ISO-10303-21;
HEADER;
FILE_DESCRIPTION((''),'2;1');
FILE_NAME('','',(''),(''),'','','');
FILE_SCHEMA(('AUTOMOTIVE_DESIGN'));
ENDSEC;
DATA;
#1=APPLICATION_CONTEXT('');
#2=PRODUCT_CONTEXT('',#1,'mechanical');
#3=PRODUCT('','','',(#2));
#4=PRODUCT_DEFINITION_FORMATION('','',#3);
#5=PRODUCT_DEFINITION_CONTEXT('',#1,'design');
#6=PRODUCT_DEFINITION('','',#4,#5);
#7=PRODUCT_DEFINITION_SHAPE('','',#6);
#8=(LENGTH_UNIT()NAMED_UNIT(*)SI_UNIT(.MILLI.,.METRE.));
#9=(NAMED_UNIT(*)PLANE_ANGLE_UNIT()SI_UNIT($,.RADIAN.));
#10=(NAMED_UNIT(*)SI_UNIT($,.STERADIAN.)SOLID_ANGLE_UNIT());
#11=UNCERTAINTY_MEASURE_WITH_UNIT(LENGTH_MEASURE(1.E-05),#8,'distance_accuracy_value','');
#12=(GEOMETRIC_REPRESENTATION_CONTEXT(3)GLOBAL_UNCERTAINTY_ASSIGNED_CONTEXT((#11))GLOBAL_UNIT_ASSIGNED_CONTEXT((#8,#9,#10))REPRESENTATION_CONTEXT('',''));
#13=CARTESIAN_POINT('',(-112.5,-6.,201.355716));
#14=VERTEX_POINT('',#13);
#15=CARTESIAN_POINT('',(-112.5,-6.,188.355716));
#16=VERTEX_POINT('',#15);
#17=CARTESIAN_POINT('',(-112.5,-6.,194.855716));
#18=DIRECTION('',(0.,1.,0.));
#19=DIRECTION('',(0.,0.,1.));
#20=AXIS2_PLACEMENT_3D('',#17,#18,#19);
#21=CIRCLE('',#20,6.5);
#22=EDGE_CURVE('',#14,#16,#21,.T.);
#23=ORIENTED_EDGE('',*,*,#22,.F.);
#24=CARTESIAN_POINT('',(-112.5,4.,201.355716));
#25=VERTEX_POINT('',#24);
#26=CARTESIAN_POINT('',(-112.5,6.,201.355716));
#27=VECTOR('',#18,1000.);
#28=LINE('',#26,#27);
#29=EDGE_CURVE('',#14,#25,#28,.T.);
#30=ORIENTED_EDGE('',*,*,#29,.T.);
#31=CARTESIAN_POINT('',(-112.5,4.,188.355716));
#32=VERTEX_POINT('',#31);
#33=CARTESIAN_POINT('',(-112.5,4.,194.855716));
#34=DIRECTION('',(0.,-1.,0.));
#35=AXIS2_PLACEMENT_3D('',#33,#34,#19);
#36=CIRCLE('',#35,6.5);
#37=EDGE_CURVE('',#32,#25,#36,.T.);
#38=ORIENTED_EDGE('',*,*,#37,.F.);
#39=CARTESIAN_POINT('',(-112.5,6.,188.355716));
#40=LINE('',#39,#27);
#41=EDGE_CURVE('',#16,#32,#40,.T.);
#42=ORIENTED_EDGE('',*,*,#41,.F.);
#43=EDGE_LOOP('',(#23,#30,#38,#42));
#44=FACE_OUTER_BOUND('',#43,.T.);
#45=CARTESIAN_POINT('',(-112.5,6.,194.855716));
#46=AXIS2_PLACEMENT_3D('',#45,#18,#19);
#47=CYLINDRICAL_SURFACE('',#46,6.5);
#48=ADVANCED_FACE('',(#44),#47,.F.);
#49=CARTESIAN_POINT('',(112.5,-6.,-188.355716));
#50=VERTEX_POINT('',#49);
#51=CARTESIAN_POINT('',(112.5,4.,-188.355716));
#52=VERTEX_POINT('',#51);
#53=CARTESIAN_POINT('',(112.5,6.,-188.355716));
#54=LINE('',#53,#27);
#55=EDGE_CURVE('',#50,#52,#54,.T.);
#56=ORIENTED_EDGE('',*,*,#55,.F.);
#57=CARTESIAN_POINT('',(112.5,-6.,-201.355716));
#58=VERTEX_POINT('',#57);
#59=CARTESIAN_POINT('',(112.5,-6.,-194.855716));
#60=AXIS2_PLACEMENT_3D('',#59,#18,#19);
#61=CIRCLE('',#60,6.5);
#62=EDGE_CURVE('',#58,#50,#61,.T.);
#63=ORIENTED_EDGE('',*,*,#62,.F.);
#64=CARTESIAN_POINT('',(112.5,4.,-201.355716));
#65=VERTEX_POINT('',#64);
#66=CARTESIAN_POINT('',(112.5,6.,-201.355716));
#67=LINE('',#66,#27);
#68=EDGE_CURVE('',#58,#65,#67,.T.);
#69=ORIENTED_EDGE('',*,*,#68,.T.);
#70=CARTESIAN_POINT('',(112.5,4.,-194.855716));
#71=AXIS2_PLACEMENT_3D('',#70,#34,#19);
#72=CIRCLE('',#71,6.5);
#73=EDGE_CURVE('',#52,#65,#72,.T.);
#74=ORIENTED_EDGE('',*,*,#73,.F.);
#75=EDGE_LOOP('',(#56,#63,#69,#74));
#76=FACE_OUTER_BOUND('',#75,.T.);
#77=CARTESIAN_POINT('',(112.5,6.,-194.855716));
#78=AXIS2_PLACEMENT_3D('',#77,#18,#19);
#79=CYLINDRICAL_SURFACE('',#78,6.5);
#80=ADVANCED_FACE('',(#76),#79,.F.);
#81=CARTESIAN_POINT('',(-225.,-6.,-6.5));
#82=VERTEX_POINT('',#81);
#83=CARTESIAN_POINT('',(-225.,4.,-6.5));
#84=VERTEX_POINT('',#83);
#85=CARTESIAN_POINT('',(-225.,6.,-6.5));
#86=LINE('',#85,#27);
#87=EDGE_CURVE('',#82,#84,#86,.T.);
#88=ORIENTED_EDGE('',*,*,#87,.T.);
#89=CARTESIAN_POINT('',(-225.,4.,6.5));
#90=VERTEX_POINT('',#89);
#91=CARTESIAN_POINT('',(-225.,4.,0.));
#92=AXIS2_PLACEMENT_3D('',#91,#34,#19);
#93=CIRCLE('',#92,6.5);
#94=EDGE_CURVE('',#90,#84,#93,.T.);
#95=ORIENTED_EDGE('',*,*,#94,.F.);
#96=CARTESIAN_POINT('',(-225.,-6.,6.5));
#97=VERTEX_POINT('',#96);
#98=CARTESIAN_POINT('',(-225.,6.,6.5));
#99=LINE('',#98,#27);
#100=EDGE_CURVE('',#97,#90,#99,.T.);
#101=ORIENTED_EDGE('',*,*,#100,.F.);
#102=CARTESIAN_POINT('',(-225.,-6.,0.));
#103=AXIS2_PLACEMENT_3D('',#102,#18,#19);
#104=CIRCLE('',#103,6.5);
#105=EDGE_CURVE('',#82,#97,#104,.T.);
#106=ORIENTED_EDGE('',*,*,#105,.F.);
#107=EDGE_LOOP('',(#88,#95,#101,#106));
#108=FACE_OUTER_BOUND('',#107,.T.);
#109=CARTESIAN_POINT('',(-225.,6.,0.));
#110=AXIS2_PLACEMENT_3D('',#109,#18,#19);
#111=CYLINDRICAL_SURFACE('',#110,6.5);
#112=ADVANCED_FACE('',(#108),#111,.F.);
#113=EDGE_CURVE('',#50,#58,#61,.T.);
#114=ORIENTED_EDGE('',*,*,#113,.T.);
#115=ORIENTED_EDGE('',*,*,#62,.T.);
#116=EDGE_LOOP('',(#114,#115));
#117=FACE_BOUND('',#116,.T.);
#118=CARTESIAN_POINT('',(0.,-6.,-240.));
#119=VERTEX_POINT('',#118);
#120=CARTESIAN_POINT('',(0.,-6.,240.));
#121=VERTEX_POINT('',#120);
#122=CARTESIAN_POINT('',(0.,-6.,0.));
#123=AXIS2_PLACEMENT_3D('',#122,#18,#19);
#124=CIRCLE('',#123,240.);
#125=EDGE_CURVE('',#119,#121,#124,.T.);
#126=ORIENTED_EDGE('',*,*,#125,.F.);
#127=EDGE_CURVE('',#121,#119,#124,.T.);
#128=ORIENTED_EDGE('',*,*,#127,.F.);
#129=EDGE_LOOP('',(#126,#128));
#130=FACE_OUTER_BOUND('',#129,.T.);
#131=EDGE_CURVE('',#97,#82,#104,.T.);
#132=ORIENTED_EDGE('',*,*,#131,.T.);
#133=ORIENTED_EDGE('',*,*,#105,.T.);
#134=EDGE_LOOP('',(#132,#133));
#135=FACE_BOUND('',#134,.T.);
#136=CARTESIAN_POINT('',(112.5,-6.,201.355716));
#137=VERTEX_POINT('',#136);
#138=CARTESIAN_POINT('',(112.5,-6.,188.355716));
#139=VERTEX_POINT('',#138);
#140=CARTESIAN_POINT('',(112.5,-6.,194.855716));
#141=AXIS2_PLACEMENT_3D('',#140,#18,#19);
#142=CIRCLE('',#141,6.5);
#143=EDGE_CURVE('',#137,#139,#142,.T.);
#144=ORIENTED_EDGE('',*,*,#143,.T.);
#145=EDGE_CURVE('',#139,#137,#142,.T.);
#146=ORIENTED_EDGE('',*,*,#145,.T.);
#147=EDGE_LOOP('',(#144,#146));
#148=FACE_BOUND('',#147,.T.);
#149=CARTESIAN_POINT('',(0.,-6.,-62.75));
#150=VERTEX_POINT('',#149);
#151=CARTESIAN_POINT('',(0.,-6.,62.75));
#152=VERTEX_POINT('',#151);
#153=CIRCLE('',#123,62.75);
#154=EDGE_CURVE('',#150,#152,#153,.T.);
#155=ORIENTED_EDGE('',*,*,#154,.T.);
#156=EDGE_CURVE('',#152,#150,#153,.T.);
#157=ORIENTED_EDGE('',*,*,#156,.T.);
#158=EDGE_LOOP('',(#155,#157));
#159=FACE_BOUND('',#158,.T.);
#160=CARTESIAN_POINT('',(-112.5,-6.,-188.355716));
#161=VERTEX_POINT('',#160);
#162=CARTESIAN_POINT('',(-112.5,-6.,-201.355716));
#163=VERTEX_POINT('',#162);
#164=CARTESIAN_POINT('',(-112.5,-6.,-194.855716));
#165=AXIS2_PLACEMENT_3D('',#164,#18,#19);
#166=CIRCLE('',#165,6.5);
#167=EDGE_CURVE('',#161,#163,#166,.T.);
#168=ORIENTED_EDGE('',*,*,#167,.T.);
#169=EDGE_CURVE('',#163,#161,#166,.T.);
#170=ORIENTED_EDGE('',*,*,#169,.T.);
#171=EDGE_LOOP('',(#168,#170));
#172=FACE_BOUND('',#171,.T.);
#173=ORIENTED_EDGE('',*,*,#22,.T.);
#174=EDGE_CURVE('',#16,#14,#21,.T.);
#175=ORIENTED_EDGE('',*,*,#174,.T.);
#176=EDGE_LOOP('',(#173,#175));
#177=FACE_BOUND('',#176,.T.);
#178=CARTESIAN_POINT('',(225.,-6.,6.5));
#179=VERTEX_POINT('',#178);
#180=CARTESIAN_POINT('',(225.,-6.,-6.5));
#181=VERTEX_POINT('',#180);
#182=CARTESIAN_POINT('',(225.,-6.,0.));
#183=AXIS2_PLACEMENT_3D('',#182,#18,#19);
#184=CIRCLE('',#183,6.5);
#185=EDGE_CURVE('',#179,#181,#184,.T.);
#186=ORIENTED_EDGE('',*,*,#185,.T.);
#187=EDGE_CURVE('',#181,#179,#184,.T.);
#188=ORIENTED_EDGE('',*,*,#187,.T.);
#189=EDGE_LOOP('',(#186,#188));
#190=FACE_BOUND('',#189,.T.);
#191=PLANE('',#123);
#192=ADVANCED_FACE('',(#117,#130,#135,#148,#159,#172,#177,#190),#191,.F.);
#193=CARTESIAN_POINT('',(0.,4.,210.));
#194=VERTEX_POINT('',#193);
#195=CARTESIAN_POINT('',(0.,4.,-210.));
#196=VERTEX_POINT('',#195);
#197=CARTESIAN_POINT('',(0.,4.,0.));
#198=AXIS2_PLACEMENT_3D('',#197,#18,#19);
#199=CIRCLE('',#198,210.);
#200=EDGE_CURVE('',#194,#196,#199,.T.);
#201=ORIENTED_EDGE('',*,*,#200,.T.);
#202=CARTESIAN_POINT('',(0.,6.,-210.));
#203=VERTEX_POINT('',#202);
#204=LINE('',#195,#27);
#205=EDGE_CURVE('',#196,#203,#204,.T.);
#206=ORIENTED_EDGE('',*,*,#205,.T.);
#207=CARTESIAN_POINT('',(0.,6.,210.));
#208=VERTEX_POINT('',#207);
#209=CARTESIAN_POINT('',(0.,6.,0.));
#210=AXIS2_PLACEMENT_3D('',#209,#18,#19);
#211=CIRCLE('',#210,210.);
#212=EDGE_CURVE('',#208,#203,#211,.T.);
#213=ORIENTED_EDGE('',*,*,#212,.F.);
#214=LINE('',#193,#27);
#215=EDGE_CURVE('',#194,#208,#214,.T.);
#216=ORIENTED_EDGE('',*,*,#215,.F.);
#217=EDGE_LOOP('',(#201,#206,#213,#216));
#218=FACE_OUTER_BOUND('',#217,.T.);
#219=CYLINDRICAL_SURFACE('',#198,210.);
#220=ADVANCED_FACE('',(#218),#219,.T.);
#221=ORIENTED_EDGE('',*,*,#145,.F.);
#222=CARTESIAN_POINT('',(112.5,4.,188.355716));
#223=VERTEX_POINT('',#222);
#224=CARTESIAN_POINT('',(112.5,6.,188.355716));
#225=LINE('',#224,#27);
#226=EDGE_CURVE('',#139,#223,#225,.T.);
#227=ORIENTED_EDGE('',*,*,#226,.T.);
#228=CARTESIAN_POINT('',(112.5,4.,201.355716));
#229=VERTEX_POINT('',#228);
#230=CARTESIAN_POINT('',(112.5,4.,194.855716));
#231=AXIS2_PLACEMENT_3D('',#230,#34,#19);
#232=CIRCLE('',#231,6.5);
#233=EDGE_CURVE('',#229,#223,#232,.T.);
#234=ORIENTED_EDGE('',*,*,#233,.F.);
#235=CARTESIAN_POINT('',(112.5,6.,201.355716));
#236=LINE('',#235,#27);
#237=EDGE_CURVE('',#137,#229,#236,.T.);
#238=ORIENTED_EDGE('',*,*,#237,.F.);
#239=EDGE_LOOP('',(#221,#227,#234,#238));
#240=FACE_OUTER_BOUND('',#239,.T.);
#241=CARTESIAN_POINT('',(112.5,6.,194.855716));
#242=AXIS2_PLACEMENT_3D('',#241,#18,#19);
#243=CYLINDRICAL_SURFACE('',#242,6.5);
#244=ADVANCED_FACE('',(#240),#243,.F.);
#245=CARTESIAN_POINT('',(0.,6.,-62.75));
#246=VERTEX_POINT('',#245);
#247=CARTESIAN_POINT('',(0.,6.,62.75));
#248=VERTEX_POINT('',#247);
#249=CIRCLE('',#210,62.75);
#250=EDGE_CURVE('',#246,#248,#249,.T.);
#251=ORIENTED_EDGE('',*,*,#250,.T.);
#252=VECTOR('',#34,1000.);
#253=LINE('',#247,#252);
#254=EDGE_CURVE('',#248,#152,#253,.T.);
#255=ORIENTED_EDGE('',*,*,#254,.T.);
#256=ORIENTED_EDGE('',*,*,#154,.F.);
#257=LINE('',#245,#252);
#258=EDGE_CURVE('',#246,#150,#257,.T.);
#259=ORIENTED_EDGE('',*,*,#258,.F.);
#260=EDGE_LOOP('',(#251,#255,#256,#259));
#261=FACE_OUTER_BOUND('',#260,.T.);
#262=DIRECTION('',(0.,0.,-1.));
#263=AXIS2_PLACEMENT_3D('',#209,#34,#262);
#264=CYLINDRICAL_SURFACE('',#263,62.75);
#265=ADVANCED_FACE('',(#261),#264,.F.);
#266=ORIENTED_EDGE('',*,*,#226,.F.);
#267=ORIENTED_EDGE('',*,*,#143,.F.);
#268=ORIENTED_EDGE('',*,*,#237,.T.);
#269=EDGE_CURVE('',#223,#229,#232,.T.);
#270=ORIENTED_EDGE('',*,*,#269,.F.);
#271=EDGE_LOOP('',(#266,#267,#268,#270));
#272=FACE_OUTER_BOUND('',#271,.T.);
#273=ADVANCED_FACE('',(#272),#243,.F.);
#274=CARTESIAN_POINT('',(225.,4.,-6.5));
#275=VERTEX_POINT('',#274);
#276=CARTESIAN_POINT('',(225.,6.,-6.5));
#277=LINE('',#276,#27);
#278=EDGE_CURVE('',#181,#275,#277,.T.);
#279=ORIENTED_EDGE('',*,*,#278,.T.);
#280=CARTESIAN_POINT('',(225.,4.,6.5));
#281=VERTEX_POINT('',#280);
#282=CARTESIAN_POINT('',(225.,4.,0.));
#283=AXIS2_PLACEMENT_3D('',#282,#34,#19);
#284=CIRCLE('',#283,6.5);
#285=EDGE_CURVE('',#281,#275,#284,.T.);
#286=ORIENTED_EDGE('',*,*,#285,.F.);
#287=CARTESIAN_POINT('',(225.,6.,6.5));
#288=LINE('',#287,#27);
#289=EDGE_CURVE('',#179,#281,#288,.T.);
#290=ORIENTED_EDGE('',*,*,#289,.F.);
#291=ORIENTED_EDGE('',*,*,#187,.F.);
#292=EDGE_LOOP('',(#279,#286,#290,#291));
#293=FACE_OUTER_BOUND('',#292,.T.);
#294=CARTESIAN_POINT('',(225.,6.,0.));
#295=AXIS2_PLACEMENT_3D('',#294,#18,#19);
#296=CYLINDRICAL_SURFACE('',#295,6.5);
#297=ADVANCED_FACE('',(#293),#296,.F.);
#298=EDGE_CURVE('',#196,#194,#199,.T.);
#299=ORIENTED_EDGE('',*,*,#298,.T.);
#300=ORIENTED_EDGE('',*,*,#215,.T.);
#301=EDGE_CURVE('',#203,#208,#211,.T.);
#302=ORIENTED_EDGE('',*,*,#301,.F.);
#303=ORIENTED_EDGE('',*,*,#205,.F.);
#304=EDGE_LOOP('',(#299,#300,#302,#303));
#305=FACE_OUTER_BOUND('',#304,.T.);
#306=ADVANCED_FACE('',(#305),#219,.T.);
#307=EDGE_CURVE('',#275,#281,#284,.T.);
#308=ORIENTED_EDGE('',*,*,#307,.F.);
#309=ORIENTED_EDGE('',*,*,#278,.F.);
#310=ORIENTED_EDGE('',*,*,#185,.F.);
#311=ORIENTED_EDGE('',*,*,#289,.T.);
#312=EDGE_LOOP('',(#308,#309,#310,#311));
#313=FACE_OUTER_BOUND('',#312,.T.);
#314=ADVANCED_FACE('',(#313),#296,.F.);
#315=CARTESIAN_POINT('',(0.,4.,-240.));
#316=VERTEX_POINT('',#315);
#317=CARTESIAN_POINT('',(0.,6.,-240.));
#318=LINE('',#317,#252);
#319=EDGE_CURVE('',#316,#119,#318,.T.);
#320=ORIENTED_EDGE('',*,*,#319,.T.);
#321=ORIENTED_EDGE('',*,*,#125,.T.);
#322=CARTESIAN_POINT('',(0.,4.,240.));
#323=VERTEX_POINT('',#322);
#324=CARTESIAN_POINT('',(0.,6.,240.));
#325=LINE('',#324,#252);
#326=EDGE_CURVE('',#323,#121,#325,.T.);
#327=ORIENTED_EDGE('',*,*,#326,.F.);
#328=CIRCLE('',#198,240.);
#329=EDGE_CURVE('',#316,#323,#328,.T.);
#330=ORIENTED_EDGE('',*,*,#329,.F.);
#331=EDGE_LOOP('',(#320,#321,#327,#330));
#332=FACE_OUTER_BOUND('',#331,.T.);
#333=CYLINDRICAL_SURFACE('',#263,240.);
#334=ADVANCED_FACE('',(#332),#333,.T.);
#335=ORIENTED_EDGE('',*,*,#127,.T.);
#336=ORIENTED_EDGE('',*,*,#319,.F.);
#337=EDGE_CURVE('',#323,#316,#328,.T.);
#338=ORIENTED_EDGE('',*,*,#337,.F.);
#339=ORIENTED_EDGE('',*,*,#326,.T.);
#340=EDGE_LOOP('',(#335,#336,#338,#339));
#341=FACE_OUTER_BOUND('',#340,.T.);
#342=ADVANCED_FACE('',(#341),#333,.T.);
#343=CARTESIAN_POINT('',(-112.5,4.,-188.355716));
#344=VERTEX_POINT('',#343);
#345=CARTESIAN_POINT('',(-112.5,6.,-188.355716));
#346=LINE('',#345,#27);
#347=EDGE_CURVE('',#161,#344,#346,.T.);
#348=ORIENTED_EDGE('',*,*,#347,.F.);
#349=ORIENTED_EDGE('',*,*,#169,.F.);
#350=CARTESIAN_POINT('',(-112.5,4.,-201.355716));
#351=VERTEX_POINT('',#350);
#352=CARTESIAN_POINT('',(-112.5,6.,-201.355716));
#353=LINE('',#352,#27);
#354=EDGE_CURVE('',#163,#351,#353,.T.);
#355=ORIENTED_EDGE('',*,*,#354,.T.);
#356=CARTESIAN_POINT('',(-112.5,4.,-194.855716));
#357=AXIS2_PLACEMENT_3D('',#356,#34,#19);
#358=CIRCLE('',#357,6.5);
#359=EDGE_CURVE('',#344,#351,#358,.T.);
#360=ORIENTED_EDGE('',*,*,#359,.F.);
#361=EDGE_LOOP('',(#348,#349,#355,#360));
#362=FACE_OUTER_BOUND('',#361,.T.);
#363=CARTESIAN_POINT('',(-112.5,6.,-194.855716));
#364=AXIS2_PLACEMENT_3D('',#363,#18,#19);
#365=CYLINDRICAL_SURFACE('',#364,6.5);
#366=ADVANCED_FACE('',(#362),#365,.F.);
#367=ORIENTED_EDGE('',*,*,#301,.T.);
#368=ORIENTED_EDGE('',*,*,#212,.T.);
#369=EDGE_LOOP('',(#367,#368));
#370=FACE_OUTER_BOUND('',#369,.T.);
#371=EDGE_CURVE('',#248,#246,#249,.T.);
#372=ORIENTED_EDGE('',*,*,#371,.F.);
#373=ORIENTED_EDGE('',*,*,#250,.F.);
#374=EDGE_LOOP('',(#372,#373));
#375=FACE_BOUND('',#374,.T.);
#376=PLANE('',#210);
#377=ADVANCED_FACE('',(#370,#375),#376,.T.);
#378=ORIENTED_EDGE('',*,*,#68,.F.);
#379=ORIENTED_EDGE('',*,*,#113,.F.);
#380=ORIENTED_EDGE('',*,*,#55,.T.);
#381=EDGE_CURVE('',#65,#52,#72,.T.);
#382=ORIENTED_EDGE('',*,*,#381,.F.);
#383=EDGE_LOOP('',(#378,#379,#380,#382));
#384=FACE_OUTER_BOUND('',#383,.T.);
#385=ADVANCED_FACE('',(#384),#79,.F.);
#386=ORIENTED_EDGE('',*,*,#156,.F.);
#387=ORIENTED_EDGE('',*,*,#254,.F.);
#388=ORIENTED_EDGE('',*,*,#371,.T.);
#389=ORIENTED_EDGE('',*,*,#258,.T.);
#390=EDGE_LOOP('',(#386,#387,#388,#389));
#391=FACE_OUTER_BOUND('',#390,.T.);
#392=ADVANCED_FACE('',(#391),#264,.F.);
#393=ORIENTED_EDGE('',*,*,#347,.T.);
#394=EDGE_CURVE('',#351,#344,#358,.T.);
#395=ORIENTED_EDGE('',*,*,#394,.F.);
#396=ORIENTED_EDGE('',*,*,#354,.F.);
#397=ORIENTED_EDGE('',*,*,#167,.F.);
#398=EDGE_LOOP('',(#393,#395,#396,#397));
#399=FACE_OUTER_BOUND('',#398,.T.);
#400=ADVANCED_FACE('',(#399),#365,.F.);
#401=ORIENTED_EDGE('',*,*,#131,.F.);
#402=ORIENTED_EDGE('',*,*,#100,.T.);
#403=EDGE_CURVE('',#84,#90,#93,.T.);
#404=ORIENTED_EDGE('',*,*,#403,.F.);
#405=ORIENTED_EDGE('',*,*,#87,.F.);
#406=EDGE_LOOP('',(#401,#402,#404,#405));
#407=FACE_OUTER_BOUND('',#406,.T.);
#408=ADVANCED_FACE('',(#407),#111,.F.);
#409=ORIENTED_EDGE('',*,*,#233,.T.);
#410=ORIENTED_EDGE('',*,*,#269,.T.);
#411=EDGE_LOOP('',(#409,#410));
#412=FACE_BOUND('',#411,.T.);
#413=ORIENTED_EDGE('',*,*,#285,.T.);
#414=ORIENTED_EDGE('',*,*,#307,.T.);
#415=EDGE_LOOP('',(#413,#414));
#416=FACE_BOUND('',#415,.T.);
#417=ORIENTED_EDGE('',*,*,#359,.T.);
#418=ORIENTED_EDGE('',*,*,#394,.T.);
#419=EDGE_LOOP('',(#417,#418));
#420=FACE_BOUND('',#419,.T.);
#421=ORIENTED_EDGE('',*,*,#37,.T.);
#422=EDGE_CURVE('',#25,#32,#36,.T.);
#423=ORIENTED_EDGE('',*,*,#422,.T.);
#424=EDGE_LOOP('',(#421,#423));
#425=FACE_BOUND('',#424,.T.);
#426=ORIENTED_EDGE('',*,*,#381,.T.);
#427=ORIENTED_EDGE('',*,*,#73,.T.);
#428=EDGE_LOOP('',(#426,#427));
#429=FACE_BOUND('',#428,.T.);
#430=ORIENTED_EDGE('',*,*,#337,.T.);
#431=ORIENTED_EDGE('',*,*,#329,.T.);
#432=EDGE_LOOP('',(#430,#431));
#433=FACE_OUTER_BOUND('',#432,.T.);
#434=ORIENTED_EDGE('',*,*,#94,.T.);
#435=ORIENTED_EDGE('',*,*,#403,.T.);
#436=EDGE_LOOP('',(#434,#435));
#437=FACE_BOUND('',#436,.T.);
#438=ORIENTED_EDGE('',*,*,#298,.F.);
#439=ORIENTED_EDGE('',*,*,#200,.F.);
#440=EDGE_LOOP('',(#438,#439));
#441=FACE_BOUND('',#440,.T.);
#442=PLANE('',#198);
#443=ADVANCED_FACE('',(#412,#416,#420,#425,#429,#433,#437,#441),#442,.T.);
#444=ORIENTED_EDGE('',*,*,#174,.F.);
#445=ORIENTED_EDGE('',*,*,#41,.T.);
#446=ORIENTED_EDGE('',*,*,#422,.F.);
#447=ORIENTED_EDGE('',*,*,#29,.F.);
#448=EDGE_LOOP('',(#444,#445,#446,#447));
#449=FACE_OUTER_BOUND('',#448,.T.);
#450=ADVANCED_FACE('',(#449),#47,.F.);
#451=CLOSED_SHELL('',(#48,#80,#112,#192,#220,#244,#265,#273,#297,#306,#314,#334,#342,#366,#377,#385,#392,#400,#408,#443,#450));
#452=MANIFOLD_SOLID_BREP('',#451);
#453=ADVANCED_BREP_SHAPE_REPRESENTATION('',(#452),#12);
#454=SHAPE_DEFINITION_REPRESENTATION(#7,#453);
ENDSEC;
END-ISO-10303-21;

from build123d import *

# Parameters (mm, degrees)
SKETCH1_R                  = 240
SKETCH1_R_2                = 62.75
BOSS_EXTRUDE1_DEPTH        = 6
F_13_0_13_DIAMETER_HOLE1_D = 13
SKETCH4_OUTSIDE_W          = 617.786
SKETCH4_OUTSIDE_H          = 617.786
SKETCH4_OUTSIDE_R          = 210
CUT_EXTRUDE1_DEPTH         = 2


with BuildPart() as part:
    # Sketch1 → Boss-Extrude1 (new, symmetric)
    with BuildSketch(Plane(origin=(0, 0, 0), x_dir=(1, 0, 0), z_dir=(0, 1, 0))):
        with Locations(Location((0, 0, 0), (0, 0, 270))):
            Circle(SKETCH1_R)
        with Locations(Location((0, 0, 0), (0, 0, 270))):
            Circle(SKETCH1_R_2, mode=Mode.SUBTRACT)
    extrude(amount=BOSS_EXTRUDE1_DEPTH, both=True)

    # Ø13.0 (13) Diameter Hole1 (through all)
    with Locations(Plane(origin=(0, 6, 0), x_dir=(1, 0, 0), z_dir=(0, 1, 0))):
        with Locations((112.5, -194.855715851), (-112.5, -194.855715851), (-225, 0), (-112.5, 194.855715851), (112.5, 194.855715851), (225, 0)):
            Hole(F_13_0_13_DIAMETER_HOLE1_D / 2)

    # Sketch4 outside → Cut-Extrude1 (cut)
    with BuildSketch(Plane(origin=(0, 6, 0), x_dir=(1, 0, 0), z_dir=(0, 1, 0))):
        Rectangle(SKETCH4_OUTSIDE_W, SKETCH4_OUTSIDE_H)
        with Locations(Location((0, 0, 0), (0, 0, 270))):
            Circle(SKETCH4_OUTSIDE_R, mode=Mode.SUBTRACT)
    extrude(amount=-CUT_EXTRUDE1_DEPTH, mode=Mode.SUBTRACT)


solid = part.part
